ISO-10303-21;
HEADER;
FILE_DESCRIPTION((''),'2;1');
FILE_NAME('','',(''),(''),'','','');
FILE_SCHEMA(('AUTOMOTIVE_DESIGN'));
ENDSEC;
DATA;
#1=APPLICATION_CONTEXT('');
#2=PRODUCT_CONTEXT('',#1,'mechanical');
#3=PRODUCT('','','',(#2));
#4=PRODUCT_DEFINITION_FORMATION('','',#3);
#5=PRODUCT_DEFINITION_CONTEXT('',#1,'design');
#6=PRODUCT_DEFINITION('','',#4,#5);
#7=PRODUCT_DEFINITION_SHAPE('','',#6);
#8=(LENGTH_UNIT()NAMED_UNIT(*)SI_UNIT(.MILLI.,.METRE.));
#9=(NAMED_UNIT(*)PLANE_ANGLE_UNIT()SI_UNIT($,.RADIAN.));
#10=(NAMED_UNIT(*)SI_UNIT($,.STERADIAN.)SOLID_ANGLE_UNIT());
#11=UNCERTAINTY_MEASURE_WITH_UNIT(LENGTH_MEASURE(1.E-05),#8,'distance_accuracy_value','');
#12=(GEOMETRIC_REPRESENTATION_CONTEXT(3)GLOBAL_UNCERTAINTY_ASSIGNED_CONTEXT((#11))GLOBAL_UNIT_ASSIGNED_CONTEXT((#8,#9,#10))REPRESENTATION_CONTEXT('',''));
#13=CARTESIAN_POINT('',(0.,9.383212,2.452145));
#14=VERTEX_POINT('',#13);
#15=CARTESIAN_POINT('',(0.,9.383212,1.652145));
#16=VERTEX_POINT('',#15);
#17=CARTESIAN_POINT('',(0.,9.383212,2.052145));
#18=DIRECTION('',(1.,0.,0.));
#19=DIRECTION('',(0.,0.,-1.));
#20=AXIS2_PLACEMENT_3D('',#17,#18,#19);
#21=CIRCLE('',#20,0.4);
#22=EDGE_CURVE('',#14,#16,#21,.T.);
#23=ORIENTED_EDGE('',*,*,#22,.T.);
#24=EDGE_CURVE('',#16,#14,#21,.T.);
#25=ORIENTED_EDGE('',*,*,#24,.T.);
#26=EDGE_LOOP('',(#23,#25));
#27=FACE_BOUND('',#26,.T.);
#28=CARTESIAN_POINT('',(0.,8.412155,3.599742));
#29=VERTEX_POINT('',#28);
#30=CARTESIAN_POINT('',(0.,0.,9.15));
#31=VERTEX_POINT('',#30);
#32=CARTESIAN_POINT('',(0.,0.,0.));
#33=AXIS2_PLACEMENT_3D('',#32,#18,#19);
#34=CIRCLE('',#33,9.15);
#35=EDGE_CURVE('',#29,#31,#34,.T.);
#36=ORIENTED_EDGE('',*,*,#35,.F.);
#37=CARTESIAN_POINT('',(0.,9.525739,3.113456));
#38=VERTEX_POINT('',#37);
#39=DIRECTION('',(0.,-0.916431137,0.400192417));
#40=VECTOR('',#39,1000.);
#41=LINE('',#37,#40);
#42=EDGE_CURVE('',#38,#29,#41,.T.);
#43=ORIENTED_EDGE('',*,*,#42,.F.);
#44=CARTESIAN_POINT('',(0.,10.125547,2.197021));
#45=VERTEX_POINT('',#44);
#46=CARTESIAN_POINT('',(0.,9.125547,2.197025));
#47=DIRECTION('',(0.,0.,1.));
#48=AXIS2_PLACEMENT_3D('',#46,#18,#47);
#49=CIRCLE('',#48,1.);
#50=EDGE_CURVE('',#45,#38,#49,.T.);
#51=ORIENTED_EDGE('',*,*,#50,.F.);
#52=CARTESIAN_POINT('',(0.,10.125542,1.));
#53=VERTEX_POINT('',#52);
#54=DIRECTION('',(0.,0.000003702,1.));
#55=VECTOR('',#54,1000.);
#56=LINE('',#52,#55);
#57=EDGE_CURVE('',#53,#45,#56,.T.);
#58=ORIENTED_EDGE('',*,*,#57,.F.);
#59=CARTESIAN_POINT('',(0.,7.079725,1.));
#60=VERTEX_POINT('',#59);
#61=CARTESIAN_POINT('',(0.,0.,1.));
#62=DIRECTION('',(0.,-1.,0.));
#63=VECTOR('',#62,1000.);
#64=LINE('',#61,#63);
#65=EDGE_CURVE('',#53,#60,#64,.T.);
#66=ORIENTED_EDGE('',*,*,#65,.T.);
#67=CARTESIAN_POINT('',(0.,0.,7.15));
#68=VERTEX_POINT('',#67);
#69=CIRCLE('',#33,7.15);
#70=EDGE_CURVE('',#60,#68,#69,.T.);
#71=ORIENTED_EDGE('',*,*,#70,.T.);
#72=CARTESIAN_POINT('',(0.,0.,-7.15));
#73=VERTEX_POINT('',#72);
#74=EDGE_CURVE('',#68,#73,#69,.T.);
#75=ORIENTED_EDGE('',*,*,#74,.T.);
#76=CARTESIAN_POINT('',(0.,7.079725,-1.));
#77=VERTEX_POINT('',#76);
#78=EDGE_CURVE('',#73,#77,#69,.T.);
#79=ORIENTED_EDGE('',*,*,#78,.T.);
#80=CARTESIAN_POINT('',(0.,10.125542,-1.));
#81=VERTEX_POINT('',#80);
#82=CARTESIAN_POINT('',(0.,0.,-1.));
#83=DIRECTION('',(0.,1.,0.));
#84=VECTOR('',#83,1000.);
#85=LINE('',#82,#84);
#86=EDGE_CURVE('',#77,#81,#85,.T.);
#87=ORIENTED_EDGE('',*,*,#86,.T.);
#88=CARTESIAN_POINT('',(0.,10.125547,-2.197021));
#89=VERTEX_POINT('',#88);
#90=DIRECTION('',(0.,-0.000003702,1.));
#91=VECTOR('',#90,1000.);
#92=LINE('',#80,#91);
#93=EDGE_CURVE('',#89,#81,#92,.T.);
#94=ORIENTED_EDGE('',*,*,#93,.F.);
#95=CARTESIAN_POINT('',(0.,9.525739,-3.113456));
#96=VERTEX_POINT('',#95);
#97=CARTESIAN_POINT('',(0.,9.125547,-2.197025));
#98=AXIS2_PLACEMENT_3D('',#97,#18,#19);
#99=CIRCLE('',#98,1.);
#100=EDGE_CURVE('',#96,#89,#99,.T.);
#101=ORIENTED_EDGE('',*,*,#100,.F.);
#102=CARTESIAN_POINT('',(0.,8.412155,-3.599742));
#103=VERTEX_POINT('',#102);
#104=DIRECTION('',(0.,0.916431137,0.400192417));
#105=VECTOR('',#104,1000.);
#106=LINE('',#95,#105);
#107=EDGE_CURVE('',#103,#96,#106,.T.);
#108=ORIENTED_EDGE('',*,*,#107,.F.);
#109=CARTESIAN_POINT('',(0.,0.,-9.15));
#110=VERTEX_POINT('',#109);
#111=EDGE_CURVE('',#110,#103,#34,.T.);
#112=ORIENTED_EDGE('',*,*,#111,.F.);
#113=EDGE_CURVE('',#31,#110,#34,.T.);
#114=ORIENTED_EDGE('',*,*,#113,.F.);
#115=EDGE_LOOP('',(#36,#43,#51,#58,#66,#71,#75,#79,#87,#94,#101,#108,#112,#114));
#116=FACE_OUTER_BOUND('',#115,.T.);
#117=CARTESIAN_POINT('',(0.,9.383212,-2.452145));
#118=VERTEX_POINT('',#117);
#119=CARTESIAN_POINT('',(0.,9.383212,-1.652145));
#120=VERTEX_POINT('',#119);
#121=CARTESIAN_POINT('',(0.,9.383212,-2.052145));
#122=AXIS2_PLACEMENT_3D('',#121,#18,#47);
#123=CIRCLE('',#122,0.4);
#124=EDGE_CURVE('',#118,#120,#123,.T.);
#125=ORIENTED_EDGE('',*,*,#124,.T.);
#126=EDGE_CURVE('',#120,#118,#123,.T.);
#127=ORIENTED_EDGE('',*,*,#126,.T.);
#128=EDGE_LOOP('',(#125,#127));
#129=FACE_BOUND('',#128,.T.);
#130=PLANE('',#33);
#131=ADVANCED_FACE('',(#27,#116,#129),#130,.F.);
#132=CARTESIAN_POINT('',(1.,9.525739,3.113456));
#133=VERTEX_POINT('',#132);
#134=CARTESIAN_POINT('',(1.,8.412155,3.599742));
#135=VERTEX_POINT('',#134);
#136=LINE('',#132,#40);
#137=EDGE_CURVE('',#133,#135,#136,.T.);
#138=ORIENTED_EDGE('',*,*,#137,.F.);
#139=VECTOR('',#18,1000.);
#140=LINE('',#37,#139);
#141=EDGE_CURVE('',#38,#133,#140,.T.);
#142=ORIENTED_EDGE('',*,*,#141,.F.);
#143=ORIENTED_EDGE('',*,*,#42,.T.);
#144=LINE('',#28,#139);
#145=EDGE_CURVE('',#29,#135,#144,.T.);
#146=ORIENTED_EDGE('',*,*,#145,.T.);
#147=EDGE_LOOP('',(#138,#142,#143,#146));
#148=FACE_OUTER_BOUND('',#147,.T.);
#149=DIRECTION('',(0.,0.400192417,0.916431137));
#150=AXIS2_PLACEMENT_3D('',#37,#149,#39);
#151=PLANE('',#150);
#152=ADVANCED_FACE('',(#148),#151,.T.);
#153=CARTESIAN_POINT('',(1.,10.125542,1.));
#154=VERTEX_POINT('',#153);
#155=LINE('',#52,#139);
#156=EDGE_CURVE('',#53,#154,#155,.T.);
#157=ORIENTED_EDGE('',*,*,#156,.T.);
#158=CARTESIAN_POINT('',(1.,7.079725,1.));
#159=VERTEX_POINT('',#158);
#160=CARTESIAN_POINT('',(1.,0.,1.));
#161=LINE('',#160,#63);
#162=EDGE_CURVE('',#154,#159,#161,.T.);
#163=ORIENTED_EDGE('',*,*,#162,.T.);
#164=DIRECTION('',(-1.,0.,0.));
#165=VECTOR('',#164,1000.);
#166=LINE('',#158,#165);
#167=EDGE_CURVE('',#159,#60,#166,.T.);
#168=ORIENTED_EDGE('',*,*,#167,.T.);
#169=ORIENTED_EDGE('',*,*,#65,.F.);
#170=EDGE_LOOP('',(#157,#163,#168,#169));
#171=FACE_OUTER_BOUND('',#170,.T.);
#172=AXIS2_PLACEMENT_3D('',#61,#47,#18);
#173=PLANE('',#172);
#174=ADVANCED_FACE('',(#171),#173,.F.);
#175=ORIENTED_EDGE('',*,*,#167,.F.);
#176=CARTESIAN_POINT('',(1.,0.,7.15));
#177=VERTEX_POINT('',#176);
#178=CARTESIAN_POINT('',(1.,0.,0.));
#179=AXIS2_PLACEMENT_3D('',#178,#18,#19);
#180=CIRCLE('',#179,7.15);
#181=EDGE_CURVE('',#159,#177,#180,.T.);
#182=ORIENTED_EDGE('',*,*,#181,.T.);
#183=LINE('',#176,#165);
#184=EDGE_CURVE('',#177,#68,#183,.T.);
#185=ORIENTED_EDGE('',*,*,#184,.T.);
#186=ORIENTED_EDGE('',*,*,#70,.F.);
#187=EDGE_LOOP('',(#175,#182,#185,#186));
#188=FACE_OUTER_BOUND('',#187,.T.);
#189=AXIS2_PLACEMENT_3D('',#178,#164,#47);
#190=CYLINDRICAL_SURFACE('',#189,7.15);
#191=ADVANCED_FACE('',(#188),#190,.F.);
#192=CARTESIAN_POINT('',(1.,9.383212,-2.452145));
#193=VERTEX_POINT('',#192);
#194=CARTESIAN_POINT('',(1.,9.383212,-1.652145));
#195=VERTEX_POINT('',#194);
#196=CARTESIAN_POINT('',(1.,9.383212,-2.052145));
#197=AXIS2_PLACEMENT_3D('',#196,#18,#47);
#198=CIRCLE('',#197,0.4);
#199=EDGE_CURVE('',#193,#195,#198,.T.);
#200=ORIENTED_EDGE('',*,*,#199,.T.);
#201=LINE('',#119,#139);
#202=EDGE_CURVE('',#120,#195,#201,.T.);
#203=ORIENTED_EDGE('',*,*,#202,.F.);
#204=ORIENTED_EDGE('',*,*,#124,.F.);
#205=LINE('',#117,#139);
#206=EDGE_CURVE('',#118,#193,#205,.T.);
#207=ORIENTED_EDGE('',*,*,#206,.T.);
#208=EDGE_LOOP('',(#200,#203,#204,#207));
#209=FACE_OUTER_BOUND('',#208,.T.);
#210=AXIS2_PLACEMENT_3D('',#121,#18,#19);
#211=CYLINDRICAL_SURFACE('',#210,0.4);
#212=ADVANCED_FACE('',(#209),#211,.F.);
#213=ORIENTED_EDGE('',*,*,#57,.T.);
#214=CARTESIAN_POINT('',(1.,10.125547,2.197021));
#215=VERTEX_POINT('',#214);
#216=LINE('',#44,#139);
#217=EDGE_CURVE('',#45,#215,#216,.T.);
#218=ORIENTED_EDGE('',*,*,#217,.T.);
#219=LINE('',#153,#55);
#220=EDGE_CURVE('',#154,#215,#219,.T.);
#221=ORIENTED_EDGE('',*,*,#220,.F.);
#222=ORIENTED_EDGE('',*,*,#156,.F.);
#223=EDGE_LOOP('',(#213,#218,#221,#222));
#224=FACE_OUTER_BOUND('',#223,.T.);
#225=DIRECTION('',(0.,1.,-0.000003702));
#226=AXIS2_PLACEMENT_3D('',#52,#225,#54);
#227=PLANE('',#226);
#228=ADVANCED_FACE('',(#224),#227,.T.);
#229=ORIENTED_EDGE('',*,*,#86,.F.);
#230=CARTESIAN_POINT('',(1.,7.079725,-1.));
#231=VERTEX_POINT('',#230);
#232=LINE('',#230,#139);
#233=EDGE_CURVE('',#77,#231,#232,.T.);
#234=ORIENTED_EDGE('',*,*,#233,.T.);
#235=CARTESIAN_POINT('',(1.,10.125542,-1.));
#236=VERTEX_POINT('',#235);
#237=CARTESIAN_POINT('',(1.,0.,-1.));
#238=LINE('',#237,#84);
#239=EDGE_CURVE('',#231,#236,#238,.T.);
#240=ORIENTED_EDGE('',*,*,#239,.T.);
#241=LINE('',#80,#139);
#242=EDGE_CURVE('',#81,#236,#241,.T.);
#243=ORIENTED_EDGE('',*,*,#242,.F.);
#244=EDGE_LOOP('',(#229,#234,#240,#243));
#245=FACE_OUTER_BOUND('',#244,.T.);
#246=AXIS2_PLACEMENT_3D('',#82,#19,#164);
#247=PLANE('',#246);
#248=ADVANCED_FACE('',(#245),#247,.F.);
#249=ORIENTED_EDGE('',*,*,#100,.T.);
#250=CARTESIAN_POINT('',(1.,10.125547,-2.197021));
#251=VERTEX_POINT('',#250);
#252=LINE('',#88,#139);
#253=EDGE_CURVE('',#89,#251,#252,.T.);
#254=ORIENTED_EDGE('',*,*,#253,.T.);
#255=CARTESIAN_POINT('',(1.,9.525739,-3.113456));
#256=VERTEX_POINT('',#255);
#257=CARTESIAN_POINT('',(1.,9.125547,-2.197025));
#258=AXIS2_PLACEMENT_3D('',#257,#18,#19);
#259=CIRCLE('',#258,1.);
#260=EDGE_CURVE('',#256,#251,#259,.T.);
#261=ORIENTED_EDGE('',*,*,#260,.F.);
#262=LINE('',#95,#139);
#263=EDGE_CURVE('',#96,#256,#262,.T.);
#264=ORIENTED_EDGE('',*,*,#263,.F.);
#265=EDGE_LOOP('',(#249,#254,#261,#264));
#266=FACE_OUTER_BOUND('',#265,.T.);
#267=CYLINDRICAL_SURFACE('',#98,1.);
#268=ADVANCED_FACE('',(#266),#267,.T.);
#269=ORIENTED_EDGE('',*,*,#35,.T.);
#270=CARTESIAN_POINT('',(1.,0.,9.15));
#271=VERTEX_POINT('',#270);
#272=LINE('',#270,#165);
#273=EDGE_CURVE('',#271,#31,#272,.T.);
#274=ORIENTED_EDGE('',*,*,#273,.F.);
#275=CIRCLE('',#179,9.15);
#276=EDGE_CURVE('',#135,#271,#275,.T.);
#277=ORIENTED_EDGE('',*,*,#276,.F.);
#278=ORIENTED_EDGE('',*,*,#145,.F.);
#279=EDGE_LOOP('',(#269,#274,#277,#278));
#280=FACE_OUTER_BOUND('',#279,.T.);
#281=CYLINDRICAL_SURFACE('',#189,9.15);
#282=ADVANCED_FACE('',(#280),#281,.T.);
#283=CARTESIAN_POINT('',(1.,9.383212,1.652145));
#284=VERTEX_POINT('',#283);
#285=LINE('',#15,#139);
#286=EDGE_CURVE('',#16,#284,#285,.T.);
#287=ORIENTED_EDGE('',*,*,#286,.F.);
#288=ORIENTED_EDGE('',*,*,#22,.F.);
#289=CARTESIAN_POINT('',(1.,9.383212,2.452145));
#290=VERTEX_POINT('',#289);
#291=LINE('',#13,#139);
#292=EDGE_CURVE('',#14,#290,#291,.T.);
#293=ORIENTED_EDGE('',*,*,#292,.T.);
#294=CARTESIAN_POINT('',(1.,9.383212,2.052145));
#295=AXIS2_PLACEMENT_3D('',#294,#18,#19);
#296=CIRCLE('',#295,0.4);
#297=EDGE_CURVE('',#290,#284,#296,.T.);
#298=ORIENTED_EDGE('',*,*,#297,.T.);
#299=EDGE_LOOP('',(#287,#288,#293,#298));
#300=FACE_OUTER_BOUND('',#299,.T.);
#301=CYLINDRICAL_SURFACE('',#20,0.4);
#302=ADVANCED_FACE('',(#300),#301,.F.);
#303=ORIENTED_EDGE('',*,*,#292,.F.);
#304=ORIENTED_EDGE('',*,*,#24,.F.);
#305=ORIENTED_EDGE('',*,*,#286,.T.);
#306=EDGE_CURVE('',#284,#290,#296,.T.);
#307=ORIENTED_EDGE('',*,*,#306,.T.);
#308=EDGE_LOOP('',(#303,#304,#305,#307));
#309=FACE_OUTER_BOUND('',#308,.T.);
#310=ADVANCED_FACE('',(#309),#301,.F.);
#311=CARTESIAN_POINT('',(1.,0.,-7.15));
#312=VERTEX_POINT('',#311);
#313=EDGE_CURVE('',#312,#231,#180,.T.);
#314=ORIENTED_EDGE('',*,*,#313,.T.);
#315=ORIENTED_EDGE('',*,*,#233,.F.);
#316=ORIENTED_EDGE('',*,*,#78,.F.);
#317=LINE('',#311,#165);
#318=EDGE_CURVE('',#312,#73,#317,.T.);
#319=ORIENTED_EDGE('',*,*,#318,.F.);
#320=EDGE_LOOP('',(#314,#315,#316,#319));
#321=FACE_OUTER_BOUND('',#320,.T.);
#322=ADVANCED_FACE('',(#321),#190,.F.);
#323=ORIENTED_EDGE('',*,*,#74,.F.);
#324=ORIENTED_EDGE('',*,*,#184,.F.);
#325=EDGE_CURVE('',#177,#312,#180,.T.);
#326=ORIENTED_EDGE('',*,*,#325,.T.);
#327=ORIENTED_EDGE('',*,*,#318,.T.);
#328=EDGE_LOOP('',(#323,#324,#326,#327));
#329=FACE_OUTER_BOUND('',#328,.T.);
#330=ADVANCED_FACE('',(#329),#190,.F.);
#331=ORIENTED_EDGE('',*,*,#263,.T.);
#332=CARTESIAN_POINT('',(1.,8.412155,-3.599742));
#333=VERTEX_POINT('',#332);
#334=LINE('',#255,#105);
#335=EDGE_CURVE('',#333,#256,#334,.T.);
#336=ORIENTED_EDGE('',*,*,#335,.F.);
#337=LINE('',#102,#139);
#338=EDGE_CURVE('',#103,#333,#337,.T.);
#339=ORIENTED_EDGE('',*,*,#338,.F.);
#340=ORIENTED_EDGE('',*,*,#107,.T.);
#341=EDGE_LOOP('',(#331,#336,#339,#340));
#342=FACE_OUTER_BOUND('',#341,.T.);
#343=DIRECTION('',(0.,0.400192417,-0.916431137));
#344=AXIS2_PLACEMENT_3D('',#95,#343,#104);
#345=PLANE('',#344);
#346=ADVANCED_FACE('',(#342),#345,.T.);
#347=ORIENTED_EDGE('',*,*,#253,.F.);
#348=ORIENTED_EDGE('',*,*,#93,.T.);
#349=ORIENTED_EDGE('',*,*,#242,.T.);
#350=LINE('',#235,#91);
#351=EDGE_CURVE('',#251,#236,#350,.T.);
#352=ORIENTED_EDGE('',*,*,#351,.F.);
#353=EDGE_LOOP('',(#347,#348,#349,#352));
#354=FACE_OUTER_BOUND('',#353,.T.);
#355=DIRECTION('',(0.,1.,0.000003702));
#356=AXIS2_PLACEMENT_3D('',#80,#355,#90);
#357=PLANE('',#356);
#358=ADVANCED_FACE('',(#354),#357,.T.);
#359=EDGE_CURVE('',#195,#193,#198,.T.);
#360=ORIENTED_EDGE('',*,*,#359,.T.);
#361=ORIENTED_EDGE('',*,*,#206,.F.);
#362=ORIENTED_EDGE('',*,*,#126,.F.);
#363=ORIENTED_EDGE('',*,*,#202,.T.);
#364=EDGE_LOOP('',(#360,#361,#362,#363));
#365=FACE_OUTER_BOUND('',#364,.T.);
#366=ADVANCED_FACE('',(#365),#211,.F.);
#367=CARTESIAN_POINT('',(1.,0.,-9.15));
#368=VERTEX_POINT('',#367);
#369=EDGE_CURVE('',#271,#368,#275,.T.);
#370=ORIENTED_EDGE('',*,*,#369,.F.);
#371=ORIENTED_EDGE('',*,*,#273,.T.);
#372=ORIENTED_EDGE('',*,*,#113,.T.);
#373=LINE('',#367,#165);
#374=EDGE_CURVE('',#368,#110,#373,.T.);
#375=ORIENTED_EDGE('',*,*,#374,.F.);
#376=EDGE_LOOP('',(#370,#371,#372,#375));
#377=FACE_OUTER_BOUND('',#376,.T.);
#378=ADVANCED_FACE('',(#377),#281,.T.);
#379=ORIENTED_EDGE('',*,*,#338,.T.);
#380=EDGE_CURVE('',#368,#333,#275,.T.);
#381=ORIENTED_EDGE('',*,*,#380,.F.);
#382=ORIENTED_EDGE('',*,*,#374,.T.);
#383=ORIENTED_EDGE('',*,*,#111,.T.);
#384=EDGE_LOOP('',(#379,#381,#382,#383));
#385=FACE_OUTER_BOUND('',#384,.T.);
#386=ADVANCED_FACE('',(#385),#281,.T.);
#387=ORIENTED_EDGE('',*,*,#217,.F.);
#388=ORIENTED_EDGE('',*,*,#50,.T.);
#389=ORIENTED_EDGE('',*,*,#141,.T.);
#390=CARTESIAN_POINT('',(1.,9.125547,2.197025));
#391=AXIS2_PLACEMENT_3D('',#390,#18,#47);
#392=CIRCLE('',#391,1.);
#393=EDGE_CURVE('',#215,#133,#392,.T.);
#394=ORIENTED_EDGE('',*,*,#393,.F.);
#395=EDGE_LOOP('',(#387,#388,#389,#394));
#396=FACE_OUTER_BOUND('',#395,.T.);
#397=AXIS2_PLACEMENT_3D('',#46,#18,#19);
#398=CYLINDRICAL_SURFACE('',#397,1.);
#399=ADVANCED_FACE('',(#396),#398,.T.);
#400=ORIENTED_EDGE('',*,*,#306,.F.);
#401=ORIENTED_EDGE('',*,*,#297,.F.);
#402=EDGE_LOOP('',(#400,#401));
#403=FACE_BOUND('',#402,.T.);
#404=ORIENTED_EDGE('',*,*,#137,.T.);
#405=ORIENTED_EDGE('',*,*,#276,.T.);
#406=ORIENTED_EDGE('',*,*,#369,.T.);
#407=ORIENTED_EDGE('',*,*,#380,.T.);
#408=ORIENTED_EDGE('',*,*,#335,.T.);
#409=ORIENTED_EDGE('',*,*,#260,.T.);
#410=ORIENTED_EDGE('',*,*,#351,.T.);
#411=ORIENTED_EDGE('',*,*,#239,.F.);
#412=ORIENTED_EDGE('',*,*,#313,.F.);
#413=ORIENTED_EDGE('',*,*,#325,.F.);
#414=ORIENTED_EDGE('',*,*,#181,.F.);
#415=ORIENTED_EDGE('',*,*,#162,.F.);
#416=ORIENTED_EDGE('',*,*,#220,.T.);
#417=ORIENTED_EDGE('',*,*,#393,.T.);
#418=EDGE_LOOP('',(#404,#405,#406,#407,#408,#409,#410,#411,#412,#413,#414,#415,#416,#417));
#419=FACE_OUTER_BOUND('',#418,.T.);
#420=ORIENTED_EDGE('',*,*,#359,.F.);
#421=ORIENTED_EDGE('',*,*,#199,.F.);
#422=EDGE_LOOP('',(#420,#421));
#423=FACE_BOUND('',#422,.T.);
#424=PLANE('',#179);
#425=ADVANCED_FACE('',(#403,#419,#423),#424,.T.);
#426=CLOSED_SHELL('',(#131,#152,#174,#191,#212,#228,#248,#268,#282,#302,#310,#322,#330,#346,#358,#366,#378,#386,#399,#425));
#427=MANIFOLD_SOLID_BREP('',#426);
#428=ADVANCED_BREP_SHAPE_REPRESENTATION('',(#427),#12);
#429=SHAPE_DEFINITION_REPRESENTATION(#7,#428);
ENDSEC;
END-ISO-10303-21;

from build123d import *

# Parameters (mm, degrees)
SKETCH_1_R          = 9.15
SKETCH_1_R_2        = 7.15
EXTRUDE_1_DEPTH     = 1
SKETCH_2_W          = 2
SKETCH_2_H          = 11.561648884
CUT_EXTRUDE_1_DEPTH = 13.978636292
EXTRUDE_START       = -1
SKETCH_3_R          = 0.4
EXTRUDE_2_DEPTH     = 1


with BuildPart() as part:
    # 草图1 → 拉伸1 (new body)
    with BuildSketch(Plane(origin=(0, 0, 0), x_dir=(0, 0, -1), z_dir=(1, 0, 0))):
        Circle(SKETCH_1_R)
        Circle(SKETCH_1_R_2, mode=Mode.SUBTRACT)
    extrude(amount=EXTRUDE_1_DEPTH)

    # 草图2 → 切除-拉伸1 (cut, through all)
    with BuildSketch(Plane(origin=(1, 0, 0), x_dir=(0, 0, -1), z_dir=(1, 0, 0))):
        with Locations((0, 5.780824442)):
            Rectangle(SKETCH_2_W, SKETCH_2_H)
    extrude(amount=-CUT_EXTRUDE_1_DEPTH, mode=Mode.SUBTRACT)

    # 草图3 → 拉伸2 (add)
    # profile 1 of 2: a face of its own
    with BuildSketch(Plane(origin=(1, 0, 0), x_dir=(0, 0, -1), z_dir=(1, 0, 0)).offset(EXTRUDE_START)):
        with BuildLine():
            Line((-1, 9.095191037), (-1, 10.12554219))
            Line((-1, 10.12554219), (-2.197020967, 10.125546621))
            ThreePointArc((-2.197020967, 10.125546621), (-2.744657845, 9.962265155), (-3.113455807, 9.525739038))
            Line((-3.113455807, 9.525739038), (-3.599741921, 8.412155378))
            ThreePointArc((-3.599741921, 8.412155378), (-2.325089431, 8.849658702), (-1, 9.095191037))
        make_face()
        with Locations((-2.0521454, 9.383212306)):
            Circle(SKETCH_3_R, mode=Mode.SUBTRACT)
    # profile 2 of 2: a face of its own
    with BuildSketch(Plane(origin=(1, 0, 0), x_dir=(0, 0, -1), z_dir=(1, 0, 0)).offset(EXTRUDE_START)):
        with BuildLine():
            Line((1, 9.095191037), (1, 10.12554219))
            Line((1, 10.12554219), (2.197020967, 10.125546621))
            ThreePointArc((2.197020967, 10.125546621), (2.744657845, 9.962265155), (3.113455807, 9.525739038))
            Line((3.113455807, 9.525739038), (3.599741921, 8.412155378))
            ThreePointArc((3.599741921, 8.412155378), (2.325089431, 8.849658702), (1, 9.095191037))
        make_face()
        with Locations(Location((2.0521454, 9.383212306, 0), (0, 0, 180))):
            Circle(SKETCH_3_R, mode=Mode.SUBTRACT)
    extrude(amount=EXTRUDE_2_DEPTH)


solid = part.part
